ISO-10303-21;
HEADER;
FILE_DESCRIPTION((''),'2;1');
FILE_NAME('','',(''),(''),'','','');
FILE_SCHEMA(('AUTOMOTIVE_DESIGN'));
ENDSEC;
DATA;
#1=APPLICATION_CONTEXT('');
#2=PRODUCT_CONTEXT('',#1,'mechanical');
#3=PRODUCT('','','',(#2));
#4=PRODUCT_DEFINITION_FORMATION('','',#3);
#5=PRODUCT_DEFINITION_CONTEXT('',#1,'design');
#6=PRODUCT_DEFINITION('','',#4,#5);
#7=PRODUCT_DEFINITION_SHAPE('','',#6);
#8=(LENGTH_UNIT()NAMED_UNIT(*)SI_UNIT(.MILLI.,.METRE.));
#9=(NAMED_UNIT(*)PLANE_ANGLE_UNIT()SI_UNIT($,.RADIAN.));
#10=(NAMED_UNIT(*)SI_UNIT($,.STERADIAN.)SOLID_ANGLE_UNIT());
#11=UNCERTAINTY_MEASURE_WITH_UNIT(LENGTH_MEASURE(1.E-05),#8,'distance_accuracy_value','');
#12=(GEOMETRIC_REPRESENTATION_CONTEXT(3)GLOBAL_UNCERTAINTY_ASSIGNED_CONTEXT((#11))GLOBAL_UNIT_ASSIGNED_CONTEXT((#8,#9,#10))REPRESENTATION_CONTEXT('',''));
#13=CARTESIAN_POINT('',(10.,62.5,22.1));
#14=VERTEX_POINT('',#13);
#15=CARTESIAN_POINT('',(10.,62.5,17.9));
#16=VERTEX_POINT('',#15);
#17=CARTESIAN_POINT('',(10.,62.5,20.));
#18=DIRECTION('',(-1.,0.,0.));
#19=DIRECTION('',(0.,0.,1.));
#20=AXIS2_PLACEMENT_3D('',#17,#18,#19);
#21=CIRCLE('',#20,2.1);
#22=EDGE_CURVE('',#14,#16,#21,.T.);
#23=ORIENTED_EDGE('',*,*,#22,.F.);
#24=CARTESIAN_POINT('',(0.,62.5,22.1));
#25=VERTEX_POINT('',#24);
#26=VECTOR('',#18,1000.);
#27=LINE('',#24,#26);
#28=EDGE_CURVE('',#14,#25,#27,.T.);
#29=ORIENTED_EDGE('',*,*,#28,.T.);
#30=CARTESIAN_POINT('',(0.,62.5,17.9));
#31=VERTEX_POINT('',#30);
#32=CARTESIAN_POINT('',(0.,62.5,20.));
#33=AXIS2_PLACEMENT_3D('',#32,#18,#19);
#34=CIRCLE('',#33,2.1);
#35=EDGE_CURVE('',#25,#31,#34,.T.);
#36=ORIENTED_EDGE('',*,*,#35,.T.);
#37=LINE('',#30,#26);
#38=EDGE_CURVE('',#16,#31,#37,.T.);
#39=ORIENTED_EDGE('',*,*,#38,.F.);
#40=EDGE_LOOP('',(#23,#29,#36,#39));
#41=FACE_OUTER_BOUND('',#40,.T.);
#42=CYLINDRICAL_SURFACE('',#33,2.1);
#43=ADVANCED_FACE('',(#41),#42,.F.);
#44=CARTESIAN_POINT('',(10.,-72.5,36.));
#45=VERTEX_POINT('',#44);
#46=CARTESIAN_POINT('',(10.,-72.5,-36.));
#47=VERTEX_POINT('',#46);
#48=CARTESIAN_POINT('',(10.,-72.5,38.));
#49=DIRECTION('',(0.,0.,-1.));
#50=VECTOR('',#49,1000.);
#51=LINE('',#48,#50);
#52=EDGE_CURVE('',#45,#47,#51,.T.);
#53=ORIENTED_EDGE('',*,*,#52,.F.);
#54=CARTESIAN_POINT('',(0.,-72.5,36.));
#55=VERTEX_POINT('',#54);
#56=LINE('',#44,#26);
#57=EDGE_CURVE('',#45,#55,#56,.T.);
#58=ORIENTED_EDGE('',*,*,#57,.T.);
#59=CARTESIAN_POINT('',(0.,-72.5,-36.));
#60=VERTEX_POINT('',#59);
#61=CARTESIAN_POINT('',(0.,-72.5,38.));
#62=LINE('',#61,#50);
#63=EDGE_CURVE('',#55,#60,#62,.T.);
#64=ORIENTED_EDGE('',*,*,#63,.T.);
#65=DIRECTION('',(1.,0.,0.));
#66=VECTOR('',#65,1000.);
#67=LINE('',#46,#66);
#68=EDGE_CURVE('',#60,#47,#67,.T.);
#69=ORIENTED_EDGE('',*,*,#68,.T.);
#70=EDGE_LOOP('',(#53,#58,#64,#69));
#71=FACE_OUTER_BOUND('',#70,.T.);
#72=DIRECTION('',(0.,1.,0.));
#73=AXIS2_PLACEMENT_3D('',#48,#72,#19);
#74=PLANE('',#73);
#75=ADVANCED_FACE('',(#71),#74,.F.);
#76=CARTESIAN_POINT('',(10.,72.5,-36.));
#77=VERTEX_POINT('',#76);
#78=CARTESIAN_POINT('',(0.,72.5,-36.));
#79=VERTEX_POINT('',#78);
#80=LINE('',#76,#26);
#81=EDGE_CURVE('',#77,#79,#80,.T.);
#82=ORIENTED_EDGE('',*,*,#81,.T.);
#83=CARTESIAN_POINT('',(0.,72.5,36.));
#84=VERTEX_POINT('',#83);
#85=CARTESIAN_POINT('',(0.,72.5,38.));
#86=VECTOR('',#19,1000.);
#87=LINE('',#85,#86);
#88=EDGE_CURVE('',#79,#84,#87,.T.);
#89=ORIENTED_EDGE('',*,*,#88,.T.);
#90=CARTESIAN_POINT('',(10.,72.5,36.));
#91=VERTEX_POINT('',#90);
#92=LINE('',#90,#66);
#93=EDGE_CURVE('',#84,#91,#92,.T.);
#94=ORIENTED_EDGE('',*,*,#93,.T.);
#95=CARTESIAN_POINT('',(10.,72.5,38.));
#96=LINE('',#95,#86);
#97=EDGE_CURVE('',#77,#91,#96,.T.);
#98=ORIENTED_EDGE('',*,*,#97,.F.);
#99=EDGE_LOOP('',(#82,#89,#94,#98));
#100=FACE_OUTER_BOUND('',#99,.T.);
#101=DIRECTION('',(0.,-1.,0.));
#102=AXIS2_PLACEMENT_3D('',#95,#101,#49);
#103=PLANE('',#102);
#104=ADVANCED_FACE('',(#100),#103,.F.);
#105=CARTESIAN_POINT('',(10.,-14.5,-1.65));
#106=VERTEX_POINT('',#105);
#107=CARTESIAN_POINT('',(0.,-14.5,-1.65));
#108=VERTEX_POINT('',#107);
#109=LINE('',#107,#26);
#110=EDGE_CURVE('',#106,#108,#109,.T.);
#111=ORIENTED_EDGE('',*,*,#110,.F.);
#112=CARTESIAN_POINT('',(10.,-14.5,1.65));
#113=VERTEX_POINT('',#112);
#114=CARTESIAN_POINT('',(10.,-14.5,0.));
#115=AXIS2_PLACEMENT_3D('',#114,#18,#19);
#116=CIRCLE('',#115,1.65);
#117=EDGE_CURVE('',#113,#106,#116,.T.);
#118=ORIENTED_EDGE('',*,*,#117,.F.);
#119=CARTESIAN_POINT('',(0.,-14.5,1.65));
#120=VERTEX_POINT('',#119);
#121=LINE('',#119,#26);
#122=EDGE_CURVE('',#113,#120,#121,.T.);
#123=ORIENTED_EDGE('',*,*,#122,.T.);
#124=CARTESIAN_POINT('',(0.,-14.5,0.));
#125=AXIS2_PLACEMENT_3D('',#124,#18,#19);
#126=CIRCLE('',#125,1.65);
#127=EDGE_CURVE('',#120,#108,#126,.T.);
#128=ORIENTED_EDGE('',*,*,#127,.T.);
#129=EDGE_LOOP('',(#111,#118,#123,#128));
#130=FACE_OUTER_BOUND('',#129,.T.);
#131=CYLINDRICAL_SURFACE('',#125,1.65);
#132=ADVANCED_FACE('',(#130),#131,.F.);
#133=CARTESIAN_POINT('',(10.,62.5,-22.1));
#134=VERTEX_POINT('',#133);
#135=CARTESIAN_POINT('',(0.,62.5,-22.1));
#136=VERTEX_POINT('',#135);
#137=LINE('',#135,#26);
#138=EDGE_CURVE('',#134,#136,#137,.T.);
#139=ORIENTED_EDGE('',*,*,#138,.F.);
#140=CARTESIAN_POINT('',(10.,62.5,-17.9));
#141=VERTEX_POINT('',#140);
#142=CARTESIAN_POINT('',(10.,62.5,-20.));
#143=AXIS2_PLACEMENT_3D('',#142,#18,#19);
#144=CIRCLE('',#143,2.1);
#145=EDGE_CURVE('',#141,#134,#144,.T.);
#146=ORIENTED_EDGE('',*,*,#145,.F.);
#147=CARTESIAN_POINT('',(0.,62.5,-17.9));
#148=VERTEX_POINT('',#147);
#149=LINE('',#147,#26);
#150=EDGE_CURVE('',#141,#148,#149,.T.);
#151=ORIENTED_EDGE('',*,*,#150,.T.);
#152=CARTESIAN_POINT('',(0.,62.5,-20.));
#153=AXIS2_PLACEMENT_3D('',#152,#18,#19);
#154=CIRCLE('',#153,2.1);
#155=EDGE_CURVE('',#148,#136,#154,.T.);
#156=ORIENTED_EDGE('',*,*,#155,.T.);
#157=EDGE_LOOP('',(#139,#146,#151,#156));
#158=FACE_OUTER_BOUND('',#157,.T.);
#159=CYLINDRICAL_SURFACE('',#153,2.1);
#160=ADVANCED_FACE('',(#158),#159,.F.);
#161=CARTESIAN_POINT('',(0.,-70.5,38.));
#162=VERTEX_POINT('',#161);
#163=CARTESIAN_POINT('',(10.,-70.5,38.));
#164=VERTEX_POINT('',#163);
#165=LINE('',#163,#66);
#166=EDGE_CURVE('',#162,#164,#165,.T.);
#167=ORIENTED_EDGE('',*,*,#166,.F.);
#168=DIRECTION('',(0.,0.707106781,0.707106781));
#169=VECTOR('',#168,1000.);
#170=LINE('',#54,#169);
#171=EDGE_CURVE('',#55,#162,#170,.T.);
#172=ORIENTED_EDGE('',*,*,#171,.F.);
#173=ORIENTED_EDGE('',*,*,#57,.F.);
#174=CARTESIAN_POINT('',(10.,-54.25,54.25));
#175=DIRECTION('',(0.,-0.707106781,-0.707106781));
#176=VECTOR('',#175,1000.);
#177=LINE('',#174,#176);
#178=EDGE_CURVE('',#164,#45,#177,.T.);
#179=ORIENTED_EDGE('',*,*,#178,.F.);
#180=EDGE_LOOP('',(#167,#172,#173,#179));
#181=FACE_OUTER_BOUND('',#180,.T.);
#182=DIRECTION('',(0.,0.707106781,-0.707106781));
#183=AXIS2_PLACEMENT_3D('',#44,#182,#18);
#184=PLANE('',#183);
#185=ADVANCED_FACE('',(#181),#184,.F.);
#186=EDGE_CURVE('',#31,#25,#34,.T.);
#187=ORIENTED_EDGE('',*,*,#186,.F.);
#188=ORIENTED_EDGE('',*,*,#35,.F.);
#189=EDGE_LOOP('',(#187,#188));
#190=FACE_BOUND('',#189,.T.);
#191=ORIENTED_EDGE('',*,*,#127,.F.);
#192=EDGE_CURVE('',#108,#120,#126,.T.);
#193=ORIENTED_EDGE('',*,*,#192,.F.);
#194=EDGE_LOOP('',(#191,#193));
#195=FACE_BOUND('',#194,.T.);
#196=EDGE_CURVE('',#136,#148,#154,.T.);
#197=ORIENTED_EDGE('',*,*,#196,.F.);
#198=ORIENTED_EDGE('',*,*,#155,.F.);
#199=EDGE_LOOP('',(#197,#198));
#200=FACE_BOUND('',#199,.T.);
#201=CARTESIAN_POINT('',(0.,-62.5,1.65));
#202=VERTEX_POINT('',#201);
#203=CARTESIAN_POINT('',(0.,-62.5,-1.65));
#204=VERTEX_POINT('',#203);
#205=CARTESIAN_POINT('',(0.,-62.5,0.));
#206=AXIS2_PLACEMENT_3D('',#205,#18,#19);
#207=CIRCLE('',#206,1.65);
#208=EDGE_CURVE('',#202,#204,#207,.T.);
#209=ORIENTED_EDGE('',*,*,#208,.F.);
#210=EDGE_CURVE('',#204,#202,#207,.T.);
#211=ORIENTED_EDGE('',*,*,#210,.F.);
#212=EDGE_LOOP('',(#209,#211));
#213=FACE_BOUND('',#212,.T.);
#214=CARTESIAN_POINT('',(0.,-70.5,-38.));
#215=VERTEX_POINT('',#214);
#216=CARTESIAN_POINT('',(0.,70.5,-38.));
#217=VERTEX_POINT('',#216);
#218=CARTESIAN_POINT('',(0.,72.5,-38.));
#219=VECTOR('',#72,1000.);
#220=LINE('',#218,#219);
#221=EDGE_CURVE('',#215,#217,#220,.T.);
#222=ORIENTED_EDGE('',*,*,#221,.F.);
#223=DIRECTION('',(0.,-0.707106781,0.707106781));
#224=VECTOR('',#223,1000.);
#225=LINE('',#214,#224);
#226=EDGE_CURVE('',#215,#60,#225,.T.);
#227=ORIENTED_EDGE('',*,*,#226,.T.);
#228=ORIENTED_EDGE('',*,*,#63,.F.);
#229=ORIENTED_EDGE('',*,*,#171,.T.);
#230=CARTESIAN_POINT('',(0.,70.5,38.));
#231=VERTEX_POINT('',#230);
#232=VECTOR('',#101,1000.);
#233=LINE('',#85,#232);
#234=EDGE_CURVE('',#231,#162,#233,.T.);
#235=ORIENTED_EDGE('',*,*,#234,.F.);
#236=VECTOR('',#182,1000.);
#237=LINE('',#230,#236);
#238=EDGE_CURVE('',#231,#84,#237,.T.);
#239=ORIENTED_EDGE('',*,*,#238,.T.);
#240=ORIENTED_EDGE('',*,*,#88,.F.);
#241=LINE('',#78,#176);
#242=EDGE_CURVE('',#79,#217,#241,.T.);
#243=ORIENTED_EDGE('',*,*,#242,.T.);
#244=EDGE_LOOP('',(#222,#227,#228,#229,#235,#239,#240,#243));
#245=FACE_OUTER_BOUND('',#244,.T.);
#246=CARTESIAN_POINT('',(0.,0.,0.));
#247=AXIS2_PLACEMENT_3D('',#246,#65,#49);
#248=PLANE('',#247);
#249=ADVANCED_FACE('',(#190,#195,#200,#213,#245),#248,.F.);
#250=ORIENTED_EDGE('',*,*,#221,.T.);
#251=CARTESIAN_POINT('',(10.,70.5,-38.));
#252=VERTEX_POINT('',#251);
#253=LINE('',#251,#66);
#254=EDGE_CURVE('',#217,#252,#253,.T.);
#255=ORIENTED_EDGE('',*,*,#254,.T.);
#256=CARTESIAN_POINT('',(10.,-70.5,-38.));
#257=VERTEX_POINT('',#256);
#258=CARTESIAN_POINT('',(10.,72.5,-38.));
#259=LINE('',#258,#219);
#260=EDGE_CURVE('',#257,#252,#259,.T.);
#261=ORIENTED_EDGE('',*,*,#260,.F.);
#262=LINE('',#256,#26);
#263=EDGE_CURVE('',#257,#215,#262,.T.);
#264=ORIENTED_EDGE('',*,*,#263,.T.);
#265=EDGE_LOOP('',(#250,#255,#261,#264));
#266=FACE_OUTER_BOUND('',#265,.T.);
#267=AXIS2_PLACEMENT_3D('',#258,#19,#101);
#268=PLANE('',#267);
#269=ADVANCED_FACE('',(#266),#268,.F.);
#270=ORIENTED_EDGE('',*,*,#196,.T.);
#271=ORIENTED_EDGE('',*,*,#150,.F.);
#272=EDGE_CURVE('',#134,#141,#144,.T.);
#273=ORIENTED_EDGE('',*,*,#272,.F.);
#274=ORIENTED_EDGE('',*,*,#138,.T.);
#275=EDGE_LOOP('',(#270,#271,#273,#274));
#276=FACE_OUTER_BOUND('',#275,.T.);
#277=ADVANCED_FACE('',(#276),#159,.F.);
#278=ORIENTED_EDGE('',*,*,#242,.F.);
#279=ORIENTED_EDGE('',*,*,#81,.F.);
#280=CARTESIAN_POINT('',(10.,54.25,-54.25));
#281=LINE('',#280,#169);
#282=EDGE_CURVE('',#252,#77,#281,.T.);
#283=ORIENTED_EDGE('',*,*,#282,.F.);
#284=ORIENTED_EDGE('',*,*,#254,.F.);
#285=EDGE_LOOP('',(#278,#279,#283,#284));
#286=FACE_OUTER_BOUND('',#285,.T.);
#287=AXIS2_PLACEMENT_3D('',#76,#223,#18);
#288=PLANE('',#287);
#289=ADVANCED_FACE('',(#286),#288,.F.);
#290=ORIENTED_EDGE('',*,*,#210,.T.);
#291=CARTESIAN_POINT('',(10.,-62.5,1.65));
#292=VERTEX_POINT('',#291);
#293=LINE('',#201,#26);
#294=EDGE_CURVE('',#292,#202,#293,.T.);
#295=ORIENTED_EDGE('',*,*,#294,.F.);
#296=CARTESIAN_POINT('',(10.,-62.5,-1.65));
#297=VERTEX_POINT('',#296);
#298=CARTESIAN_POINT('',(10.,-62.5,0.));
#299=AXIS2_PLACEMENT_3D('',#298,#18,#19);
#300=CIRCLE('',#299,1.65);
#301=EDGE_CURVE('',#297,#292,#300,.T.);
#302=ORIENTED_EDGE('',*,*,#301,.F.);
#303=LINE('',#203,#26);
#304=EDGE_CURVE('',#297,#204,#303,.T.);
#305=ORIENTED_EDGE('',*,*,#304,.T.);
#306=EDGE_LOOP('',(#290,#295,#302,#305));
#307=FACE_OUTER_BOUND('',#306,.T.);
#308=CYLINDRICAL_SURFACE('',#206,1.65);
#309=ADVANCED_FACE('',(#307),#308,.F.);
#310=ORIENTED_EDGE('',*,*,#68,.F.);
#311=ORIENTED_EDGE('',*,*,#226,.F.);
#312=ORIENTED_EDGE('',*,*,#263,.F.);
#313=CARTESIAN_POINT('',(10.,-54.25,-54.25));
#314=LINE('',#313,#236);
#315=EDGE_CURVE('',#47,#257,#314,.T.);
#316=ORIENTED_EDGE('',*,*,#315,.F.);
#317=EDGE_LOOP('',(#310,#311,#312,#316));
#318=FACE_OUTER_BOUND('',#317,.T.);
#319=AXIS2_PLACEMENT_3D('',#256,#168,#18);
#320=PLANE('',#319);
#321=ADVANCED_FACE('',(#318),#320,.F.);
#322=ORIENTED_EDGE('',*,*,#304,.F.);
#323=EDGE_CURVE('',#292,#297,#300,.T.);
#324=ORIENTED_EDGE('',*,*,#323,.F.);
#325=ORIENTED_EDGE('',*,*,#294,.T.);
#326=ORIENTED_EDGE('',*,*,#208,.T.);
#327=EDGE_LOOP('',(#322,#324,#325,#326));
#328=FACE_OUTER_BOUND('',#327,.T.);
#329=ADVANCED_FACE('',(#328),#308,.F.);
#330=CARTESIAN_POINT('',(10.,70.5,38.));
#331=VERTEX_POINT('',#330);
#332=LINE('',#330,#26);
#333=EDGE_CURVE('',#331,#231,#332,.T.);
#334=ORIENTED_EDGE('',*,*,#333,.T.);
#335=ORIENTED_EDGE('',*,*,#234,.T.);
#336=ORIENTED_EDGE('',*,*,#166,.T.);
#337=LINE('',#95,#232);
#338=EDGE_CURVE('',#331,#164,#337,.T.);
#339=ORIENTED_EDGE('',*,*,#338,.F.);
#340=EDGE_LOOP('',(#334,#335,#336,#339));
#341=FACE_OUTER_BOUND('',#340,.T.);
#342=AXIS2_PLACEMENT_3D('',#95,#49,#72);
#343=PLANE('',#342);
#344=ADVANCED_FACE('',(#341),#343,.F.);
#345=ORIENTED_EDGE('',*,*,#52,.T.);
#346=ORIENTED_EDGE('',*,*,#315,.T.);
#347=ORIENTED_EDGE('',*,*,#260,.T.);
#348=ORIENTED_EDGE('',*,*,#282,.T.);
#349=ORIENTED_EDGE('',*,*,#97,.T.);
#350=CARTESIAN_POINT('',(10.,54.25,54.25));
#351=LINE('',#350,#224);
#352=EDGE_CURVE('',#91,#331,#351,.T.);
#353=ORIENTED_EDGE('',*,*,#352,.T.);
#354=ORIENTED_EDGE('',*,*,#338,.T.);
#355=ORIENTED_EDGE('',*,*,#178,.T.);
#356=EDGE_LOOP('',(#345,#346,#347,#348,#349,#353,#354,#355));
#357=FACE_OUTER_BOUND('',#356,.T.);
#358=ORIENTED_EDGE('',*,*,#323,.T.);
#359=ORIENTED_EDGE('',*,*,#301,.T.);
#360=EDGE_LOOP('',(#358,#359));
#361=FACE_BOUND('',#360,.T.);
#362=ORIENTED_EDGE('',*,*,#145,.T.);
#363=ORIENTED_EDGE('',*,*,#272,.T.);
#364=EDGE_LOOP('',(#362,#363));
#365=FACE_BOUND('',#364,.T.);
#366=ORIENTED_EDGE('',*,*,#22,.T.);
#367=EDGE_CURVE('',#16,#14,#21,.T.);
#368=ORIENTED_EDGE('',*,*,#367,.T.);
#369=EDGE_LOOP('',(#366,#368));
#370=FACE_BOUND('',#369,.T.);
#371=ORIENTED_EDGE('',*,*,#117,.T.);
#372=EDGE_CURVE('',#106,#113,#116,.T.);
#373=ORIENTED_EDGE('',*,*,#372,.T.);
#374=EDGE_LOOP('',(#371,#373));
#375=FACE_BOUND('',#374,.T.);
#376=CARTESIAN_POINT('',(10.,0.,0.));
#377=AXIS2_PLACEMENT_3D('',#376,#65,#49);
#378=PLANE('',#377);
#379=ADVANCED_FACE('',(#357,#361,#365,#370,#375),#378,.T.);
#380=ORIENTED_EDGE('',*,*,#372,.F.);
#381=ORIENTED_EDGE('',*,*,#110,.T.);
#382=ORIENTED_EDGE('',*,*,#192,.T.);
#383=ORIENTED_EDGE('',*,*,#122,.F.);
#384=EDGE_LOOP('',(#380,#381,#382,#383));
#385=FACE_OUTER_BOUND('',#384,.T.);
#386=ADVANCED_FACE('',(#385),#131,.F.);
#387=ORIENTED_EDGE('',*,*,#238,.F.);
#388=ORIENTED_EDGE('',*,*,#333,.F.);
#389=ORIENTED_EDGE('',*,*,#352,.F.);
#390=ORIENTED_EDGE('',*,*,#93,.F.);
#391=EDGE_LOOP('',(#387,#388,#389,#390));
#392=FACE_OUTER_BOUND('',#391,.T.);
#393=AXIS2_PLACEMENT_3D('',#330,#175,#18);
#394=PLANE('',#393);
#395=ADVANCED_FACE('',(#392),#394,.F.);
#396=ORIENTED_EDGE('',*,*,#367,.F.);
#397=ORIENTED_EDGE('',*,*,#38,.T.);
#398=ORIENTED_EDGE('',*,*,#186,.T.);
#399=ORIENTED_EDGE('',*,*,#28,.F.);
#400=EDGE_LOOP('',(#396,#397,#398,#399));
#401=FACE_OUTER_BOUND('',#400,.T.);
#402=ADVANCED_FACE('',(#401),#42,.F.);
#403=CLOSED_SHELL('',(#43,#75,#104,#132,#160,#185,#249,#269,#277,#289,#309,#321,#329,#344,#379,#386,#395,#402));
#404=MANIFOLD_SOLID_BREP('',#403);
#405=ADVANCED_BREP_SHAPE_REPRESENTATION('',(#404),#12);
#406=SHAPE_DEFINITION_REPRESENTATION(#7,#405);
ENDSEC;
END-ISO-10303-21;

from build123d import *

# Parameters (mm, degrees)
SKETCH_1_W         = 76
SKETCH_1_H         = 145
EXTRUDE_1_DEPTH    = 10
HOLE_WIZARD_M5_1_D = 4.2
HOLE_WIZARD_M4_1_D = 3.3
CHAMFER_1_SIZE     = 2


with BuildPart() as part:
    # 草图1 → 凸台-拉伸1 (new body)
    with BuildSketch(Plane(origin=(0, 0, 0), x_dir=(0, 0, -1), z_dir=(1, 0, 0))):
        Rectangle(SKETCH_1_W, SKETCH_1_H)
    extrude(amount=EXTRUDE_1_DEPTH)

    # M5 螺纹孔1 (through all)
    with Locations(Plane.ZY):
        with Locations((20, 62.5), (-20, 62.5)):
            Hole(HOLE_WIZARD_M5_1_D / 2)

    # M4 螺纹孔1 (through all)
    with Locations(Plane.ZY):
        with Locations((0, -14.5), (0, -62.5)):
            Hole(HOLE_WIZARD_M4_1_D / 2)

    # 倒角1
    chamfer_1_edges = [part.edges().sort_by_distance(p)[0] for p in [
        (5, -72.5, -38),
        (5, -72.5, 38),
        (5, 72.5, 38),
        (5, 72.5, -38),
    ]]
    chamfer(chamfer_1_edges, length=CHAMFER_1_SIZE)


solid = part.part
